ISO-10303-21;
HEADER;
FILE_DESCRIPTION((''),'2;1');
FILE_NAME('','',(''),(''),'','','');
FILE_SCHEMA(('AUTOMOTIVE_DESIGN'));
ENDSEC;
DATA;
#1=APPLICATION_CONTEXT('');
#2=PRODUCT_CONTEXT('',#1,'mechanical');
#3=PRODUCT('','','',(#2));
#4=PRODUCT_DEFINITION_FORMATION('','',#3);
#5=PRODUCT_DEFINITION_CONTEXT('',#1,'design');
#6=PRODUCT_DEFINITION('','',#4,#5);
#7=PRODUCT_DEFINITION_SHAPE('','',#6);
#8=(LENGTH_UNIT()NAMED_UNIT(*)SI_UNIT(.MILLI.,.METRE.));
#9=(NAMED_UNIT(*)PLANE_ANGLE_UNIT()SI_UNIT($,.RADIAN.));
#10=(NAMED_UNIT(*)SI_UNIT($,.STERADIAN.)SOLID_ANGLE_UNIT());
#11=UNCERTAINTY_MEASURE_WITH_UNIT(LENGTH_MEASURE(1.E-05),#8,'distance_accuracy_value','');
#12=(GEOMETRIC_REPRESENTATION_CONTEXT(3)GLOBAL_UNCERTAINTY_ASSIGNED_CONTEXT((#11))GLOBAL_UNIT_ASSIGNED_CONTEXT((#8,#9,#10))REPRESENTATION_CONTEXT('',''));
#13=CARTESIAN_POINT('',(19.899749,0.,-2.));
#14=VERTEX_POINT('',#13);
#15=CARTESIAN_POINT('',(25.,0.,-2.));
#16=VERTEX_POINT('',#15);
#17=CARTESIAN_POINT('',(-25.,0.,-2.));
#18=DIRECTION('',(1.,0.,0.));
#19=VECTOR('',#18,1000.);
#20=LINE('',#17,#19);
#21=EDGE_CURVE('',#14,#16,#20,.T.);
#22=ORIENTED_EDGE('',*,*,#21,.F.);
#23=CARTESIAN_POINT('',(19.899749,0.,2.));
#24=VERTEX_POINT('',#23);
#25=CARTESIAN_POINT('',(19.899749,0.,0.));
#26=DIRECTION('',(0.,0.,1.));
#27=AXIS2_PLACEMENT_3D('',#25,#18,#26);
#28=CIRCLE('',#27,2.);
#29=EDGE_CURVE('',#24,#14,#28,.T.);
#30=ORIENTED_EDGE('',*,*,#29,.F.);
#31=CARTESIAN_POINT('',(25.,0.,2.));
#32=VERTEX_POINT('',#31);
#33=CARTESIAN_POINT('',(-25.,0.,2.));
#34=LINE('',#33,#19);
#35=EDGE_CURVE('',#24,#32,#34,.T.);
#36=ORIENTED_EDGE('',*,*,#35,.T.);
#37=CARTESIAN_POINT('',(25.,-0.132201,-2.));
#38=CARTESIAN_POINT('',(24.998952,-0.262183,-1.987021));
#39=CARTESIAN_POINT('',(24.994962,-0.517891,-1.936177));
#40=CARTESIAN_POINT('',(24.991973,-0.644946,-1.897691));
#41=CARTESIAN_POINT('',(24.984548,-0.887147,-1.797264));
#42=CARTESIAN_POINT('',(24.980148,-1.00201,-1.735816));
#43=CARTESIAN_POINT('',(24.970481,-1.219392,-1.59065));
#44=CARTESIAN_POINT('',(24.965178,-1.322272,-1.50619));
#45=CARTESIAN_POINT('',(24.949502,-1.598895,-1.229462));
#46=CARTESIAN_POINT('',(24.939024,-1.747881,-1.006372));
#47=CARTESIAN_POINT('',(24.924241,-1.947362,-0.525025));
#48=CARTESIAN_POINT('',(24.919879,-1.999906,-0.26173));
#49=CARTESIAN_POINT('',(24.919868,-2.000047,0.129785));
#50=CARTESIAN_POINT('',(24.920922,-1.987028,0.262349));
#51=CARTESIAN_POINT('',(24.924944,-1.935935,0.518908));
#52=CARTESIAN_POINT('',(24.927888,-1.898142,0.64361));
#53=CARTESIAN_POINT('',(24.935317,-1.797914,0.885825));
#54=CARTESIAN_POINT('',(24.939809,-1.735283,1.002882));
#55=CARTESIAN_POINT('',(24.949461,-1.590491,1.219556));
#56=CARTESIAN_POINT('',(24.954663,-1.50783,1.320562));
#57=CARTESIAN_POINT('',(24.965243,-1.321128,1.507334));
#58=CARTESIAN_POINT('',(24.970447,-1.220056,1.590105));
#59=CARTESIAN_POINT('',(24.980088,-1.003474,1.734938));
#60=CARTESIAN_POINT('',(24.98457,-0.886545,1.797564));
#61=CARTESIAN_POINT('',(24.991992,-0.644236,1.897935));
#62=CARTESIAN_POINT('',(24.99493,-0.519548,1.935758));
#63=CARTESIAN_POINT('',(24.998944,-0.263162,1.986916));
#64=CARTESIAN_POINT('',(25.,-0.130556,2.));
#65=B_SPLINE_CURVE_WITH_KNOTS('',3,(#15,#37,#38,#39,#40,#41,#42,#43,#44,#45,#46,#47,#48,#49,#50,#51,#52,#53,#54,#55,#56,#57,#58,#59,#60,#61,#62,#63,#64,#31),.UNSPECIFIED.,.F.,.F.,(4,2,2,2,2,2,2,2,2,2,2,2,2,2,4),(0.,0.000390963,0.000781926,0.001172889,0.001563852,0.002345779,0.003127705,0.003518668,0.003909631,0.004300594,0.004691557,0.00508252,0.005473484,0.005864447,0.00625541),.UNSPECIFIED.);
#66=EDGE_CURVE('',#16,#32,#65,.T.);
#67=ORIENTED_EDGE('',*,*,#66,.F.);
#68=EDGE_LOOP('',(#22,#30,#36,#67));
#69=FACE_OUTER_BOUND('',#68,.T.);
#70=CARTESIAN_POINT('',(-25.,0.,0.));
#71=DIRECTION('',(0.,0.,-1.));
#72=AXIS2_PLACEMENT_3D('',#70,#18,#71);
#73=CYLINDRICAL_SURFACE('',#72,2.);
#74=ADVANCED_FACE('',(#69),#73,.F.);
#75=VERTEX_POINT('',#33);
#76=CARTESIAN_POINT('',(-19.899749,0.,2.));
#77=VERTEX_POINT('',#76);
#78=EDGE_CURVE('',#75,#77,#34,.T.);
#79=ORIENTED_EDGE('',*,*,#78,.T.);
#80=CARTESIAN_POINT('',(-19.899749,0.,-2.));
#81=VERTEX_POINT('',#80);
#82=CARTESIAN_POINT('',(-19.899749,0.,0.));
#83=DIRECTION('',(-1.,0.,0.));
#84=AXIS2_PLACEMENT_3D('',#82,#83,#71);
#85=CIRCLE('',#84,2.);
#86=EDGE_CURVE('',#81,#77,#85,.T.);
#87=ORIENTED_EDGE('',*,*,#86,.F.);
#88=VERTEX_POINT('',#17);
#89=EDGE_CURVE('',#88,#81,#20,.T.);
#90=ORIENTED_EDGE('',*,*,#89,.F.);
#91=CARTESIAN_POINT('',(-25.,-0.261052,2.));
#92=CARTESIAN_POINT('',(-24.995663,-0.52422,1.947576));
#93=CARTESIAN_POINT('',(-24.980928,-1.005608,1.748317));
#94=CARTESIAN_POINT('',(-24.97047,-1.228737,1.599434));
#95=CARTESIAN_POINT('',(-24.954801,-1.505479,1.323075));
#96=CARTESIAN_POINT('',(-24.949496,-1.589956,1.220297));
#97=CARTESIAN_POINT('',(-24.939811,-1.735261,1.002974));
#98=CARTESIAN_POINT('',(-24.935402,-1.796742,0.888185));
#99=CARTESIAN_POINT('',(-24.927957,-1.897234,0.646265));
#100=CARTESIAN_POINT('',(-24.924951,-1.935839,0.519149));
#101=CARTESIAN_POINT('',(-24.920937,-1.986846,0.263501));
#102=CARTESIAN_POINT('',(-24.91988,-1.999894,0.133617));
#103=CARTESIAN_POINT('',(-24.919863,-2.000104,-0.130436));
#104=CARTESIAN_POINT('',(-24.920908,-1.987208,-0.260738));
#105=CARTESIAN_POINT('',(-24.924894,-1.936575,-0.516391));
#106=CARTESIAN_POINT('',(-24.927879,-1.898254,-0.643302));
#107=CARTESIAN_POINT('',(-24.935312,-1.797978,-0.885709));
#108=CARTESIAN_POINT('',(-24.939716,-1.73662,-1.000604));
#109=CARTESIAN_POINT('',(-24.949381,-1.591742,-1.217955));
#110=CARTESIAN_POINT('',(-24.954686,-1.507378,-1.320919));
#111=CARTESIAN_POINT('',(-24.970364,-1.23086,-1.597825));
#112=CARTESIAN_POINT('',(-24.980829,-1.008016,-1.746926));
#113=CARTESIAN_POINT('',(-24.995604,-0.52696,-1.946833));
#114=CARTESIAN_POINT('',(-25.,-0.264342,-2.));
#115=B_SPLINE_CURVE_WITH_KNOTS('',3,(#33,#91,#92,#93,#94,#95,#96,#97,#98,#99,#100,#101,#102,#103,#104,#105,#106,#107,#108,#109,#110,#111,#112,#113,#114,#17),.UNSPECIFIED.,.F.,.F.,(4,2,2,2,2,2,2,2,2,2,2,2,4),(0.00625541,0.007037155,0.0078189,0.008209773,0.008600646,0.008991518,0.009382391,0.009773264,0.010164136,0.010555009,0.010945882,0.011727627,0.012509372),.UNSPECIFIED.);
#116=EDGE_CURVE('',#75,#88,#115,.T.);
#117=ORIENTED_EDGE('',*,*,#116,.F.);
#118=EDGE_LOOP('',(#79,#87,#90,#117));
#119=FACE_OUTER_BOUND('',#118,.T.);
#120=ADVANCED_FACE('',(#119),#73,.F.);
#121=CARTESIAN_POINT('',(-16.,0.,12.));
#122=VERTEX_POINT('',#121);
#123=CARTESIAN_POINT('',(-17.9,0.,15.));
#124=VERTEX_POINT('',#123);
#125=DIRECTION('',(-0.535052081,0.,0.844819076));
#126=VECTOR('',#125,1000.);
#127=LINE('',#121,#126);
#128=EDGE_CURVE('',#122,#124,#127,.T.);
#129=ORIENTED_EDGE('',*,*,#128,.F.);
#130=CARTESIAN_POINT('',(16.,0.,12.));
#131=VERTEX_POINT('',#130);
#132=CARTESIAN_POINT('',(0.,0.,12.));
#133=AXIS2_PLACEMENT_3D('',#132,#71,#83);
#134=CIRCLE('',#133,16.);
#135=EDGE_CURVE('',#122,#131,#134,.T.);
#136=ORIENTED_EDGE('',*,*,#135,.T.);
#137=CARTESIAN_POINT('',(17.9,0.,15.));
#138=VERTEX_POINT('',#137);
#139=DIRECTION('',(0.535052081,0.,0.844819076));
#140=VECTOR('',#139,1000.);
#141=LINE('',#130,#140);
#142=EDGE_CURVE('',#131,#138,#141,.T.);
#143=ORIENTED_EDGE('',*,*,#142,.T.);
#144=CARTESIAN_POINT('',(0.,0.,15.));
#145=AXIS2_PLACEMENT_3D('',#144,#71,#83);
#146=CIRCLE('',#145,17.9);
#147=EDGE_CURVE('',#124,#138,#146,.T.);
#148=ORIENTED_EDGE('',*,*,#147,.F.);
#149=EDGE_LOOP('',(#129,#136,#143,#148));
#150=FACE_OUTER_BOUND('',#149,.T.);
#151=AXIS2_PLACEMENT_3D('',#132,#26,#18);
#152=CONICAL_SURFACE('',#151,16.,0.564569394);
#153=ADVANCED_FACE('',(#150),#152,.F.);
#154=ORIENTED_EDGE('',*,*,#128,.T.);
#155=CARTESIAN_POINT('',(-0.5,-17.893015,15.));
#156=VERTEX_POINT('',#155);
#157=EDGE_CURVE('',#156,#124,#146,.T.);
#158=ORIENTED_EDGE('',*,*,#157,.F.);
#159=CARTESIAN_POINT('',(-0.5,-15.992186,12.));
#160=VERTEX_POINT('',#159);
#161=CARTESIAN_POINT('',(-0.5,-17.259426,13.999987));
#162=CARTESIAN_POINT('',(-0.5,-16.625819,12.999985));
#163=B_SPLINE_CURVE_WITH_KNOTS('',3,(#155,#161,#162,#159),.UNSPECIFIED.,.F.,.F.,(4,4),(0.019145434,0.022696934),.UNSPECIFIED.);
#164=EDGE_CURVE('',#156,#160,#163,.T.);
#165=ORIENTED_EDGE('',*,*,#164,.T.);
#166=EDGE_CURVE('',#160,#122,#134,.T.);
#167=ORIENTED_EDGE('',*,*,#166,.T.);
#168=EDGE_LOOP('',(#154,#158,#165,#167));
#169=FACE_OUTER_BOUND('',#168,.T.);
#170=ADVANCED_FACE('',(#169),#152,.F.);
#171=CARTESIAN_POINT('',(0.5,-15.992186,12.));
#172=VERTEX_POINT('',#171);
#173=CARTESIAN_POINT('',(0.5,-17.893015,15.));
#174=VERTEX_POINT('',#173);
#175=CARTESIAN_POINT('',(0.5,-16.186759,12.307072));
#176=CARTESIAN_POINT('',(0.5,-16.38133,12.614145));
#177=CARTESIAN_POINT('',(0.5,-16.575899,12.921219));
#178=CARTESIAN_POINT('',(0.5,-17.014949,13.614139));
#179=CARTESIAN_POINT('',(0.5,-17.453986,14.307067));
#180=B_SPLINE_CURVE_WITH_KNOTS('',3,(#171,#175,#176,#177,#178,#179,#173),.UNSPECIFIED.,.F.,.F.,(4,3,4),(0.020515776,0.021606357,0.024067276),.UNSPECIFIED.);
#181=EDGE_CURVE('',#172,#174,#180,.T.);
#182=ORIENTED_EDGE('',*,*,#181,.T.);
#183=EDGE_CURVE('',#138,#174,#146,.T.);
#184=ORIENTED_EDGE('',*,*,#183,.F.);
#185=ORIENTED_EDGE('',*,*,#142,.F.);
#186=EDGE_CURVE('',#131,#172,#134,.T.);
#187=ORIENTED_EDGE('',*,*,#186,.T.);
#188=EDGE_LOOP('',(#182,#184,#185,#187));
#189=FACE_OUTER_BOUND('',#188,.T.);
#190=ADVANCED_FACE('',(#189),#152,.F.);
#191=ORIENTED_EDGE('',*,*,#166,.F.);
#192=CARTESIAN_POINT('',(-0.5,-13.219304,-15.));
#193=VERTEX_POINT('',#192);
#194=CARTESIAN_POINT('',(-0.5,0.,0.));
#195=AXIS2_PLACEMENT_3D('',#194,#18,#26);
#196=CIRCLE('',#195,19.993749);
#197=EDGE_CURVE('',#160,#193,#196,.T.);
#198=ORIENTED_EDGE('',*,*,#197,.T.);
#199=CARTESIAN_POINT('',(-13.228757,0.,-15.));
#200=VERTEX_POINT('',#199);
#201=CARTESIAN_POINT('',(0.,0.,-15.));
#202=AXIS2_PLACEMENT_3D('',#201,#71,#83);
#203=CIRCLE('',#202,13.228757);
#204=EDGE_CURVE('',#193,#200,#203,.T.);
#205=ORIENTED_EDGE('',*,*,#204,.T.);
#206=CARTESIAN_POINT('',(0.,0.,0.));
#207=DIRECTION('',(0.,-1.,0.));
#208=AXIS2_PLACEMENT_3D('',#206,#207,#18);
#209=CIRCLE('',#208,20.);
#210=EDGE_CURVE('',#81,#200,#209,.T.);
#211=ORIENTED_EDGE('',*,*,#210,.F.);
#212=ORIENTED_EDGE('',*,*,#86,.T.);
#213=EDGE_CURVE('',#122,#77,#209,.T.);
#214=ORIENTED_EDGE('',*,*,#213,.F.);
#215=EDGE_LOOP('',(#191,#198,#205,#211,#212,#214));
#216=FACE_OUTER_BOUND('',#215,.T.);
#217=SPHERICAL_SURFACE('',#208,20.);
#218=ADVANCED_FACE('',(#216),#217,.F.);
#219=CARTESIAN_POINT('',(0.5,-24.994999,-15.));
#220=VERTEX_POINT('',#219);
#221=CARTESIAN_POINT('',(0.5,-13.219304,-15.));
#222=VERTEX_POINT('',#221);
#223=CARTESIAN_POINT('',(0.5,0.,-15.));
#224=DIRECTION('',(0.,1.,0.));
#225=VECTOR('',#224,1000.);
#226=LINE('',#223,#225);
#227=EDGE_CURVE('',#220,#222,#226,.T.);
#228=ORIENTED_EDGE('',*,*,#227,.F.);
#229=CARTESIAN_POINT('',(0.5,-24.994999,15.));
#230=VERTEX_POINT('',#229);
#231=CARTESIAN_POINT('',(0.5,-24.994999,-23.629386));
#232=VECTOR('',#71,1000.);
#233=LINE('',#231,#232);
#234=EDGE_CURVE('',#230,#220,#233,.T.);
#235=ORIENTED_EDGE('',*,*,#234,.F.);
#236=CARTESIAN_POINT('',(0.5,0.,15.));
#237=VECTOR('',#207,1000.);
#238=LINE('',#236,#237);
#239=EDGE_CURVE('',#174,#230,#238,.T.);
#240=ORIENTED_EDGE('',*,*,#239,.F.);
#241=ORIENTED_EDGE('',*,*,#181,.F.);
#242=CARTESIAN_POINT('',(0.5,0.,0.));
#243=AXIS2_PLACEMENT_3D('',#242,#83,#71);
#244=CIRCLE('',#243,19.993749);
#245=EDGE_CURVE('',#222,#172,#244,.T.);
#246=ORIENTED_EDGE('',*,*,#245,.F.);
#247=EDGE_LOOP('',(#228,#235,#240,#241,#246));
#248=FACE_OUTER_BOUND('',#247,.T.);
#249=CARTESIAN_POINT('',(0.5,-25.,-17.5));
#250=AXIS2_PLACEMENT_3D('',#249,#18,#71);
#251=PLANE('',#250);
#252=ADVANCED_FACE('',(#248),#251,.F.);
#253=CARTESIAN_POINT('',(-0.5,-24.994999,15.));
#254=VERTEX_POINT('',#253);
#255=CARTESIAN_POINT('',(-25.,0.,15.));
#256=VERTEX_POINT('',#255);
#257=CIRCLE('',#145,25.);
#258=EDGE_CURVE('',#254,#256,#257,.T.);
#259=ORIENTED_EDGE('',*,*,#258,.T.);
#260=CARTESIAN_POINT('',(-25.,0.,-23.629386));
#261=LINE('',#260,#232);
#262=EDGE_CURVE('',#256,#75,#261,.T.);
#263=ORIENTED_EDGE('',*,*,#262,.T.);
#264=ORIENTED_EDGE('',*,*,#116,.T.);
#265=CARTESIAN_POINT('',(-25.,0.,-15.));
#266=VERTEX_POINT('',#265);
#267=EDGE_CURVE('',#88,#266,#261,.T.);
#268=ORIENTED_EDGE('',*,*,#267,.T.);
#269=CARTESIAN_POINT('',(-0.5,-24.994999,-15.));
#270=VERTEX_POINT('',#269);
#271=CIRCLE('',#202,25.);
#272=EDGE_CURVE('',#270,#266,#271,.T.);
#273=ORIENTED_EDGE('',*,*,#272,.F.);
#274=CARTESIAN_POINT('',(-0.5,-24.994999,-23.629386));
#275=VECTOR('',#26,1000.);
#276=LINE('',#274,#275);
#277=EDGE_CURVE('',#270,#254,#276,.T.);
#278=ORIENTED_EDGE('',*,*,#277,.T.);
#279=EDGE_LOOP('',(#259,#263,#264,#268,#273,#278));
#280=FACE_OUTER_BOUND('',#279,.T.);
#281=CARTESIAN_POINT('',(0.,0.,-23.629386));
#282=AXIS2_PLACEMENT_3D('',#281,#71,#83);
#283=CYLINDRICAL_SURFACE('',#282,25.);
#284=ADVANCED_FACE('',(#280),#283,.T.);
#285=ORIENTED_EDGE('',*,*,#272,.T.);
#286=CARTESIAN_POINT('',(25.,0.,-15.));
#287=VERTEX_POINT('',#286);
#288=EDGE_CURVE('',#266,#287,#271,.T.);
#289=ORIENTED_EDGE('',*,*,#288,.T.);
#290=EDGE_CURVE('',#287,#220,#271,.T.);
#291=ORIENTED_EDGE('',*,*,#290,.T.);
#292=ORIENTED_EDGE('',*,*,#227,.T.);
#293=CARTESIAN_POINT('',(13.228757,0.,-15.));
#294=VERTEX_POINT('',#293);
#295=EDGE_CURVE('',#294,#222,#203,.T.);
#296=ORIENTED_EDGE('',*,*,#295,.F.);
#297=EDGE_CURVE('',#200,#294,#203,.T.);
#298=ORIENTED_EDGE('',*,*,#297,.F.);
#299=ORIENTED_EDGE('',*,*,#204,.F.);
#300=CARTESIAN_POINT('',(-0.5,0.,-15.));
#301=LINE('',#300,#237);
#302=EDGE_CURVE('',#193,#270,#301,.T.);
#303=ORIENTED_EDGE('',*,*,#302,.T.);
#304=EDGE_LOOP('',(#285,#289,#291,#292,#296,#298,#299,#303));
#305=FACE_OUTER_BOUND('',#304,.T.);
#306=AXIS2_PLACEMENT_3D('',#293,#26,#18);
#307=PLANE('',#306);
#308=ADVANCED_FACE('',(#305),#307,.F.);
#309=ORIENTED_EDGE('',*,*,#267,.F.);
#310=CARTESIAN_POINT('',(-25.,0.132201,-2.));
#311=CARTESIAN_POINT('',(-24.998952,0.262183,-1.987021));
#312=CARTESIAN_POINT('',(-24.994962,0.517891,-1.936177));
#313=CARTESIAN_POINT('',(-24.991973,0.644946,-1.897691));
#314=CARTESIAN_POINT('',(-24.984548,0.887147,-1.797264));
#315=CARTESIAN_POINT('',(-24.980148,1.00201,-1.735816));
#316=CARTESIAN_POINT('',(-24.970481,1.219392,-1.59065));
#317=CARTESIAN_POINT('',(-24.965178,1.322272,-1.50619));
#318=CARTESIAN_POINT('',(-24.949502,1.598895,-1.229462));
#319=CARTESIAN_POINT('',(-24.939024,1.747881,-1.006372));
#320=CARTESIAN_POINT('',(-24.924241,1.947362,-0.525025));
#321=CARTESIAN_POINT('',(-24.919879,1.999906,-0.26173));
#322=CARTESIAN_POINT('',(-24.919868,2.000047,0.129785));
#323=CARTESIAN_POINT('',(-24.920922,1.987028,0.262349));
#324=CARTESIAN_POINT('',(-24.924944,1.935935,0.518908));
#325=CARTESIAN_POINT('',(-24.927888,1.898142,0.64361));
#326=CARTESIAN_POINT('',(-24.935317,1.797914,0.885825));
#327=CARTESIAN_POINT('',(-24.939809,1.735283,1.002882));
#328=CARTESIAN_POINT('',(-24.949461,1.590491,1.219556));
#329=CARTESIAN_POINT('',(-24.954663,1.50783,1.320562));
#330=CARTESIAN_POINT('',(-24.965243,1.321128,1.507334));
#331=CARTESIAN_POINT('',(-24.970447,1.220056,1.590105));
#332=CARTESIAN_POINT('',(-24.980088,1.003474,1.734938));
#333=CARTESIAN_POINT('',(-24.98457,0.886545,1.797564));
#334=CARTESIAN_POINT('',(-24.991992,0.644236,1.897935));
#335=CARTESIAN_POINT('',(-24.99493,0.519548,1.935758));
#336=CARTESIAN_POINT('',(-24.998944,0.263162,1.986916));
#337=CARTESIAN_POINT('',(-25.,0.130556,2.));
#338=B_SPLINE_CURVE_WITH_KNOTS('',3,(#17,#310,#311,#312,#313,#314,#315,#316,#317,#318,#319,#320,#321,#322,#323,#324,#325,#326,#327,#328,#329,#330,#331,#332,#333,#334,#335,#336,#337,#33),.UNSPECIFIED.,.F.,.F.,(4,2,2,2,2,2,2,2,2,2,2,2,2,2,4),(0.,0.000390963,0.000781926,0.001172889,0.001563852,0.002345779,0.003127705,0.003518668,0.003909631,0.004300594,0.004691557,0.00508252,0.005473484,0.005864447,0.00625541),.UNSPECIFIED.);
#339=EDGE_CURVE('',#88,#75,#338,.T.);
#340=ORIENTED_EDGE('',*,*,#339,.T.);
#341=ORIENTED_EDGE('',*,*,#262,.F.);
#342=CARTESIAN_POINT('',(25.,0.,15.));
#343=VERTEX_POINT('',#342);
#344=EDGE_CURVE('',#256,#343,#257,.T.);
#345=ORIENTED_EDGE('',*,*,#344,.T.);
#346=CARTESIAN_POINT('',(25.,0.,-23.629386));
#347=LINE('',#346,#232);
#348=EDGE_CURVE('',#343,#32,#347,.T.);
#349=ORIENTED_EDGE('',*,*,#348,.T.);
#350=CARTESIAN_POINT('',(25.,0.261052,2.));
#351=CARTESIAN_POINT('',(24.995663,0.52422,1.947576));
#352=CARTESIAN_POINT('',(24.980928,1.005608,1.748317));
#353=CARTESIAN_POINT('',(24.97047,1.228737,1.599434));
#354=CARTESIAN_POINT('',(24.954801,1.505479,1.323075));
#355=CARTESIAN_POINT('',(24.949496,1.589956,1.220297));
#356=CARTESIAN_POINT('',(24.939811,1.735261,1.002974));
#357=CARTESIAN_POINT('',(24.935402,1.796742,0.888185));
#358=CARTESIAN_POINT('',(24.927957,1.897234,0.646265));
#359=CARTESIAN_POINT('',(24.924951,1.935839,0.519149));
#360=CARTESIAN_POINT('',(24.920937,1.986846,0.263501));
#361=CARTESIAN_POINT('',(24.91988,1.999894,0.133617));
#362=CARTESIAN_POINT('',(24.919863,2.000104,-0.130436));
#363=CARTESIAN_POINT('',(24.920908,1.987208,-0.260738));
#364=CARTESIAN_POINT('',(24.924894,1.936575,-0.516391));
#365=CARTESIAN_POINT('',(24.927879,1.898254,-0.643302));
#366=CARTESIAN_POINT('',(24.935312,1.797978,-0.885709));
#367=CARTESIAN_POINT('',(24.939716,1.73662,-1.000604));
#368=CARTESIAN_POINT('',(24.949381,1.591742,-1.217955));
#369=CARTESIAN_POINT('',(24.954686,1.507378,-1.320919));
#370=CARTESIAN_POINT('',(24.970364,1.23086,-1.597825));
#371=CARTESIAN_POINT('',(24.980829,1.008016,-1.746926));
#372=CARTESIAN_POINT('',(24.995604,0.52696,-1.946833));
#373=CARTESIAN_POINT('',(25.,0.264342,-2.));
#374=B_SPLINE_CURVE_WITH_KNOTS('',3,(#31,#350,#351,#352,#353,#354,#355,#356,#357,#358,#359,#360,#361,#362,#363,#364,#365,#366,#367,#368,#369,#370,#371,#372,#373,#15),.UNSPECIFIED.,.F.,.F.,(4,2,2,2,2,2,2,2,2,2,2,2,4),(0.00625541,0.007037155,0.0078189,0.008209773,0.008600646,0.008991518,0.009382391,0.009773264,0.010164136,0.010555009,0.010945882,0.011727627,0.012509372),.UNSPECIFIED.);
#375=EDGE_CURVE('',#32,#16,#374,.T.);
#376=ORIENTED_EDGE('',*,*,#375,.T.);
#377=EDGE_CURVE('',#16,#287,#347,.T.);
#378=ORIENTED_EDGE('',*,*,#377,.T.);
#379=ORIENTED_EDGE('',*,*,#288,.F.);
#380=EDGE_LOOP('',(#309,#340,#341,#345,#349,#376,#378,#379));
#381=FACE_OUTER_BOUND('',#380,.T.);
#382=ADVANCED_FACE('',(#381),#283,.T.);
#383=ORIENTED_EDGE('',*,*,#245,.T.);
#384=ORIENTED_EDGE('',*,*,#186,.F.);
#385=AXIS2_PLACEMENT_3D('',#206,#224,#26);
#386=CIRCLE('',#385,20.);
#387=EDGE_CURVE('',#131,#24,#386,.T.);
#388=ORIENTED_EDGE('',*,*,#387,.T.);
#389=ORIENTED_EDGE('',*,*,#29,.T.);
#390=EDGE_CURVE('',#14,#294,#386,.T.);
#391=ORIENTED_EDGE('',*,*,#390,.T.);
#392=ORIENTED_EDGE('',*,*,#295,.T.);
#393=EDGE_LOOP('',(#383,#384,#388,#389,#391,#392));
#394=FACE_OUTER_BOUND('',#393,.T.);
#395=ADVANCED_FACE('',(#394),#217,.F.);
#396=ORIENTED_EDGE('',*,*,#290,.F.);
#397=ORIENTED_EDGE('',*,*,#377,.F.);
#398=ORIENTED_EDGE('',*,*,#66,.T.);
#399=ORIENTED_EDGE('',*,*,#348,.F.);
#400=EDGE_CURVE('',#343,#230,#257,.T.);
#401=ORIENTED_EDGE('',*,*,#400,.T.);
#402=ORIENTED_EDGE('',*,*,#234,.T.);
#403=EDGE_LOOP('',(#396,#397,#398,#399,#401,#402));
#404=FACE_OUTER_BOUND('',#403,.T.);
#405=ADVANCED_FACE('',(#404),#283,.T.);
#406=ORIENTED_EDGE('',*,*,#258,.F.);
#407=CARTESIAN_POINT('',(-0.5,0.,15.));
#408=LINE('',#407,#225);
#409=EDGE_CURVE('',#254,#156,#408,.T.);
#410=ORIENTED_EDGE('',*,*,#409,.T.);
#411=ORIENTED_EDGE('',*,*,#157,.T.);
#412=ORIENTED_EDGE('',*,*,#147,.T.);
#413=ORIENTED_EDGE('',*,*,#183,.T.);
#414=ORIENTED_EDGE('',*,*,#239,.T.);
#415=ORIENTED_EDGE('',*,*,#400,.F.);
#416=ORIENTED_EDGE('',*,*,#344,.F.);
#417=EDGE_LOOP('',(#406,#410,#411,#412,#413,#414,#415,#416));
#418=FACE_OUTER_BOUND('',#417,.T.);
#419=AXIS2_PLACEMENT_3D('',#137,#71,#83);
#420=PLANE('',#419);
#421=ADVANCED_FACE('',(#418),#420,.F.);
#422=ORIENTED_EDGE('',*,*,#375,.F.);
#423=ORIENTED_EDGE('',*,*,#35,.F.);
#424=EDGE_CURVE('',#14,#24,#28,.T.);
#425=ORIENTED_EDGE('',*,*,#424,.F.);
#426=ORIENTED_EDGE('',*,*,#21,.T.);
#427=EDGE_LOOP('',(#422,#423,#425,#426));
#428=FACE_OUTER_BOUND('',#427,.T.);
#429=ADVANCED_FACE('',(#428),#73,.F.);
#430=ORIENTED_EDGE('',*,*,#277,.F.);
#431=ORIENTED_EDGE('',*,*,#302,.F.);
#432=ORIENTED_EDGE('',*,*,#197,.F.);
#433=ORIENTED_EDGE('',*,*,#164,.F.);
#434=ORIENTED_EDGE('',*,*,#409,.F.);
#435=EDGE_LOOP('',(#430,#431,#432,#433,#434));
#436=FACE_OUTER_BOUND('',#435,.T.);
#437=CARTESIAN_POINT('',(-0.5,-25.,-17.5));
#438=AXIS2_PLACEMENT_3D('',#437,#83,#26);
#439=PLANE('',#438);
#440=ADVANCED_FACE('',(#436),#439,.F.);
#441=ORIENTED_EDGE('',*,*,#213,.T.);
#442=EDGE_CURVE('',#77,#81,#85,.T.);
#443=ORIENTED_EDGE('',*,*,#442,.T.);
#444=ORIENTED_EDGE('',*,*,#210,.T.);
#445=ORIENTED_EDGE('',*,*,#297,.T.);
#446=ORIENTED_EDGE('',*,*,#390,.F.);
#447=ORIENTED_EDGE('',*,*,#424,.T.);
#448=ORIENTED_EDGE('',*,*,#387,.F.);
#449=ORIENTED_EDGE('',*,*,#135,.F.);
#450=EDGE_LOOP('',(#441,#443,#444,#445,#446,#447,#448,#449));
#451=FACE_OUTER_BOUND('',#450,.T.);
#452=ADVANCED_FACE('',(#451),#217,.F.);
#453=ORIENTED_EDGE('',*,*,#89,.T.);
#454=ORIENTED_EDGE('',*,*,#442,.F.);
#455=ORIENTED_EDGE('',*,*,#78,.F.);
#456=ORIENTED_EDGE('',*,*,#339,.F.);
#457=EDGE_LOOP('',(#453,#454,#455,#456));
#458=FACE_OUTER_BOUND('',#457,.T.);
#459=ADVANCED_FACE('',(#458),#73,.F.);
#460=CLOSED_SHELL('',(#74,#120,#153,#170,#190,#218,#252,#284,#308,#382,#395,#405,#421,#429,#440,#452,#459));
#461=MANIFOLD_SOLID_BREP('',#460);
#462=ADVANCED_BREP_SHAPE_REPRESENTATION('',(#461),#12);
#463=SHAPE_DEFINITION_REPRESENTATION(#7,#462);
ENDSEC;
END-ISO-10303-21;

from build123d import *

# Parameters (mm, degrees)
SKETCH_2_W               = 1
SKETCH_2_H               = 35
CUT_EXTRUDE_1_DEPTH      = 39.405728739
CUT_EXTRUDE_2_DEPTH      = 39.405728739
CUT_EXTRUDE_2_DEPTH_BACK = 39.405728739
SKETCH_3_R               = 2


with BuildPart() as part:
    # 草图1 → 旋转1 (revolve)
    with BuildSketch(Plane(origin=(0, 0, 0), x_dir=(1, 0, 0), z_dir=(0, 1, 0))):
        with BuildLine():
            Line((17.9, -15), (16, -12))
            ThreePointArc((16, -12), (19.895478191, 2.042044945), (13.228756555, 15))
            Line((13.228756555, 15), (25, 15))
            Line((25, 15), (25, -15))
            Line((25, -15), (17.9, -15))
        make_face()
    revolve(axis=Axis((0, 0, -23.629385965), (0, 0, 1)))

    # 草图2 → 切除-拉伸1 (cut, through all)
    with BuildSketch(Plane(origin=(0, 0, 0), x_dir=(1, 0, 0), z_dir=(0, 1, 0))):
        Rectangle(SKETCH_2_W, SKETCH_2_H)
    extrude(amount=-CUT_EXTRUDE_1_DEPTH, mode=Mode.SUBTRACT)

    # 草图3 → 切除-拉伸2 (cut, two sides: drawn at the far end of the back side and taken through both)
    with BuildSketch(Plane(origin=(0, 0, 0), x_dir=(0, 0, -1), z_dir=(1, 0, 0)).offset(-CUT_EXTRUDE_2_DEPTH_BACK)):
        Circle(SKETCH_3_R)
    extrude(amount=CUT_EXTRUDE_2_DEPTH + CUT_EXTRUDE_2_DEPTH_BACK, mode=Mode.SUBTRACT)


solid = part.part
